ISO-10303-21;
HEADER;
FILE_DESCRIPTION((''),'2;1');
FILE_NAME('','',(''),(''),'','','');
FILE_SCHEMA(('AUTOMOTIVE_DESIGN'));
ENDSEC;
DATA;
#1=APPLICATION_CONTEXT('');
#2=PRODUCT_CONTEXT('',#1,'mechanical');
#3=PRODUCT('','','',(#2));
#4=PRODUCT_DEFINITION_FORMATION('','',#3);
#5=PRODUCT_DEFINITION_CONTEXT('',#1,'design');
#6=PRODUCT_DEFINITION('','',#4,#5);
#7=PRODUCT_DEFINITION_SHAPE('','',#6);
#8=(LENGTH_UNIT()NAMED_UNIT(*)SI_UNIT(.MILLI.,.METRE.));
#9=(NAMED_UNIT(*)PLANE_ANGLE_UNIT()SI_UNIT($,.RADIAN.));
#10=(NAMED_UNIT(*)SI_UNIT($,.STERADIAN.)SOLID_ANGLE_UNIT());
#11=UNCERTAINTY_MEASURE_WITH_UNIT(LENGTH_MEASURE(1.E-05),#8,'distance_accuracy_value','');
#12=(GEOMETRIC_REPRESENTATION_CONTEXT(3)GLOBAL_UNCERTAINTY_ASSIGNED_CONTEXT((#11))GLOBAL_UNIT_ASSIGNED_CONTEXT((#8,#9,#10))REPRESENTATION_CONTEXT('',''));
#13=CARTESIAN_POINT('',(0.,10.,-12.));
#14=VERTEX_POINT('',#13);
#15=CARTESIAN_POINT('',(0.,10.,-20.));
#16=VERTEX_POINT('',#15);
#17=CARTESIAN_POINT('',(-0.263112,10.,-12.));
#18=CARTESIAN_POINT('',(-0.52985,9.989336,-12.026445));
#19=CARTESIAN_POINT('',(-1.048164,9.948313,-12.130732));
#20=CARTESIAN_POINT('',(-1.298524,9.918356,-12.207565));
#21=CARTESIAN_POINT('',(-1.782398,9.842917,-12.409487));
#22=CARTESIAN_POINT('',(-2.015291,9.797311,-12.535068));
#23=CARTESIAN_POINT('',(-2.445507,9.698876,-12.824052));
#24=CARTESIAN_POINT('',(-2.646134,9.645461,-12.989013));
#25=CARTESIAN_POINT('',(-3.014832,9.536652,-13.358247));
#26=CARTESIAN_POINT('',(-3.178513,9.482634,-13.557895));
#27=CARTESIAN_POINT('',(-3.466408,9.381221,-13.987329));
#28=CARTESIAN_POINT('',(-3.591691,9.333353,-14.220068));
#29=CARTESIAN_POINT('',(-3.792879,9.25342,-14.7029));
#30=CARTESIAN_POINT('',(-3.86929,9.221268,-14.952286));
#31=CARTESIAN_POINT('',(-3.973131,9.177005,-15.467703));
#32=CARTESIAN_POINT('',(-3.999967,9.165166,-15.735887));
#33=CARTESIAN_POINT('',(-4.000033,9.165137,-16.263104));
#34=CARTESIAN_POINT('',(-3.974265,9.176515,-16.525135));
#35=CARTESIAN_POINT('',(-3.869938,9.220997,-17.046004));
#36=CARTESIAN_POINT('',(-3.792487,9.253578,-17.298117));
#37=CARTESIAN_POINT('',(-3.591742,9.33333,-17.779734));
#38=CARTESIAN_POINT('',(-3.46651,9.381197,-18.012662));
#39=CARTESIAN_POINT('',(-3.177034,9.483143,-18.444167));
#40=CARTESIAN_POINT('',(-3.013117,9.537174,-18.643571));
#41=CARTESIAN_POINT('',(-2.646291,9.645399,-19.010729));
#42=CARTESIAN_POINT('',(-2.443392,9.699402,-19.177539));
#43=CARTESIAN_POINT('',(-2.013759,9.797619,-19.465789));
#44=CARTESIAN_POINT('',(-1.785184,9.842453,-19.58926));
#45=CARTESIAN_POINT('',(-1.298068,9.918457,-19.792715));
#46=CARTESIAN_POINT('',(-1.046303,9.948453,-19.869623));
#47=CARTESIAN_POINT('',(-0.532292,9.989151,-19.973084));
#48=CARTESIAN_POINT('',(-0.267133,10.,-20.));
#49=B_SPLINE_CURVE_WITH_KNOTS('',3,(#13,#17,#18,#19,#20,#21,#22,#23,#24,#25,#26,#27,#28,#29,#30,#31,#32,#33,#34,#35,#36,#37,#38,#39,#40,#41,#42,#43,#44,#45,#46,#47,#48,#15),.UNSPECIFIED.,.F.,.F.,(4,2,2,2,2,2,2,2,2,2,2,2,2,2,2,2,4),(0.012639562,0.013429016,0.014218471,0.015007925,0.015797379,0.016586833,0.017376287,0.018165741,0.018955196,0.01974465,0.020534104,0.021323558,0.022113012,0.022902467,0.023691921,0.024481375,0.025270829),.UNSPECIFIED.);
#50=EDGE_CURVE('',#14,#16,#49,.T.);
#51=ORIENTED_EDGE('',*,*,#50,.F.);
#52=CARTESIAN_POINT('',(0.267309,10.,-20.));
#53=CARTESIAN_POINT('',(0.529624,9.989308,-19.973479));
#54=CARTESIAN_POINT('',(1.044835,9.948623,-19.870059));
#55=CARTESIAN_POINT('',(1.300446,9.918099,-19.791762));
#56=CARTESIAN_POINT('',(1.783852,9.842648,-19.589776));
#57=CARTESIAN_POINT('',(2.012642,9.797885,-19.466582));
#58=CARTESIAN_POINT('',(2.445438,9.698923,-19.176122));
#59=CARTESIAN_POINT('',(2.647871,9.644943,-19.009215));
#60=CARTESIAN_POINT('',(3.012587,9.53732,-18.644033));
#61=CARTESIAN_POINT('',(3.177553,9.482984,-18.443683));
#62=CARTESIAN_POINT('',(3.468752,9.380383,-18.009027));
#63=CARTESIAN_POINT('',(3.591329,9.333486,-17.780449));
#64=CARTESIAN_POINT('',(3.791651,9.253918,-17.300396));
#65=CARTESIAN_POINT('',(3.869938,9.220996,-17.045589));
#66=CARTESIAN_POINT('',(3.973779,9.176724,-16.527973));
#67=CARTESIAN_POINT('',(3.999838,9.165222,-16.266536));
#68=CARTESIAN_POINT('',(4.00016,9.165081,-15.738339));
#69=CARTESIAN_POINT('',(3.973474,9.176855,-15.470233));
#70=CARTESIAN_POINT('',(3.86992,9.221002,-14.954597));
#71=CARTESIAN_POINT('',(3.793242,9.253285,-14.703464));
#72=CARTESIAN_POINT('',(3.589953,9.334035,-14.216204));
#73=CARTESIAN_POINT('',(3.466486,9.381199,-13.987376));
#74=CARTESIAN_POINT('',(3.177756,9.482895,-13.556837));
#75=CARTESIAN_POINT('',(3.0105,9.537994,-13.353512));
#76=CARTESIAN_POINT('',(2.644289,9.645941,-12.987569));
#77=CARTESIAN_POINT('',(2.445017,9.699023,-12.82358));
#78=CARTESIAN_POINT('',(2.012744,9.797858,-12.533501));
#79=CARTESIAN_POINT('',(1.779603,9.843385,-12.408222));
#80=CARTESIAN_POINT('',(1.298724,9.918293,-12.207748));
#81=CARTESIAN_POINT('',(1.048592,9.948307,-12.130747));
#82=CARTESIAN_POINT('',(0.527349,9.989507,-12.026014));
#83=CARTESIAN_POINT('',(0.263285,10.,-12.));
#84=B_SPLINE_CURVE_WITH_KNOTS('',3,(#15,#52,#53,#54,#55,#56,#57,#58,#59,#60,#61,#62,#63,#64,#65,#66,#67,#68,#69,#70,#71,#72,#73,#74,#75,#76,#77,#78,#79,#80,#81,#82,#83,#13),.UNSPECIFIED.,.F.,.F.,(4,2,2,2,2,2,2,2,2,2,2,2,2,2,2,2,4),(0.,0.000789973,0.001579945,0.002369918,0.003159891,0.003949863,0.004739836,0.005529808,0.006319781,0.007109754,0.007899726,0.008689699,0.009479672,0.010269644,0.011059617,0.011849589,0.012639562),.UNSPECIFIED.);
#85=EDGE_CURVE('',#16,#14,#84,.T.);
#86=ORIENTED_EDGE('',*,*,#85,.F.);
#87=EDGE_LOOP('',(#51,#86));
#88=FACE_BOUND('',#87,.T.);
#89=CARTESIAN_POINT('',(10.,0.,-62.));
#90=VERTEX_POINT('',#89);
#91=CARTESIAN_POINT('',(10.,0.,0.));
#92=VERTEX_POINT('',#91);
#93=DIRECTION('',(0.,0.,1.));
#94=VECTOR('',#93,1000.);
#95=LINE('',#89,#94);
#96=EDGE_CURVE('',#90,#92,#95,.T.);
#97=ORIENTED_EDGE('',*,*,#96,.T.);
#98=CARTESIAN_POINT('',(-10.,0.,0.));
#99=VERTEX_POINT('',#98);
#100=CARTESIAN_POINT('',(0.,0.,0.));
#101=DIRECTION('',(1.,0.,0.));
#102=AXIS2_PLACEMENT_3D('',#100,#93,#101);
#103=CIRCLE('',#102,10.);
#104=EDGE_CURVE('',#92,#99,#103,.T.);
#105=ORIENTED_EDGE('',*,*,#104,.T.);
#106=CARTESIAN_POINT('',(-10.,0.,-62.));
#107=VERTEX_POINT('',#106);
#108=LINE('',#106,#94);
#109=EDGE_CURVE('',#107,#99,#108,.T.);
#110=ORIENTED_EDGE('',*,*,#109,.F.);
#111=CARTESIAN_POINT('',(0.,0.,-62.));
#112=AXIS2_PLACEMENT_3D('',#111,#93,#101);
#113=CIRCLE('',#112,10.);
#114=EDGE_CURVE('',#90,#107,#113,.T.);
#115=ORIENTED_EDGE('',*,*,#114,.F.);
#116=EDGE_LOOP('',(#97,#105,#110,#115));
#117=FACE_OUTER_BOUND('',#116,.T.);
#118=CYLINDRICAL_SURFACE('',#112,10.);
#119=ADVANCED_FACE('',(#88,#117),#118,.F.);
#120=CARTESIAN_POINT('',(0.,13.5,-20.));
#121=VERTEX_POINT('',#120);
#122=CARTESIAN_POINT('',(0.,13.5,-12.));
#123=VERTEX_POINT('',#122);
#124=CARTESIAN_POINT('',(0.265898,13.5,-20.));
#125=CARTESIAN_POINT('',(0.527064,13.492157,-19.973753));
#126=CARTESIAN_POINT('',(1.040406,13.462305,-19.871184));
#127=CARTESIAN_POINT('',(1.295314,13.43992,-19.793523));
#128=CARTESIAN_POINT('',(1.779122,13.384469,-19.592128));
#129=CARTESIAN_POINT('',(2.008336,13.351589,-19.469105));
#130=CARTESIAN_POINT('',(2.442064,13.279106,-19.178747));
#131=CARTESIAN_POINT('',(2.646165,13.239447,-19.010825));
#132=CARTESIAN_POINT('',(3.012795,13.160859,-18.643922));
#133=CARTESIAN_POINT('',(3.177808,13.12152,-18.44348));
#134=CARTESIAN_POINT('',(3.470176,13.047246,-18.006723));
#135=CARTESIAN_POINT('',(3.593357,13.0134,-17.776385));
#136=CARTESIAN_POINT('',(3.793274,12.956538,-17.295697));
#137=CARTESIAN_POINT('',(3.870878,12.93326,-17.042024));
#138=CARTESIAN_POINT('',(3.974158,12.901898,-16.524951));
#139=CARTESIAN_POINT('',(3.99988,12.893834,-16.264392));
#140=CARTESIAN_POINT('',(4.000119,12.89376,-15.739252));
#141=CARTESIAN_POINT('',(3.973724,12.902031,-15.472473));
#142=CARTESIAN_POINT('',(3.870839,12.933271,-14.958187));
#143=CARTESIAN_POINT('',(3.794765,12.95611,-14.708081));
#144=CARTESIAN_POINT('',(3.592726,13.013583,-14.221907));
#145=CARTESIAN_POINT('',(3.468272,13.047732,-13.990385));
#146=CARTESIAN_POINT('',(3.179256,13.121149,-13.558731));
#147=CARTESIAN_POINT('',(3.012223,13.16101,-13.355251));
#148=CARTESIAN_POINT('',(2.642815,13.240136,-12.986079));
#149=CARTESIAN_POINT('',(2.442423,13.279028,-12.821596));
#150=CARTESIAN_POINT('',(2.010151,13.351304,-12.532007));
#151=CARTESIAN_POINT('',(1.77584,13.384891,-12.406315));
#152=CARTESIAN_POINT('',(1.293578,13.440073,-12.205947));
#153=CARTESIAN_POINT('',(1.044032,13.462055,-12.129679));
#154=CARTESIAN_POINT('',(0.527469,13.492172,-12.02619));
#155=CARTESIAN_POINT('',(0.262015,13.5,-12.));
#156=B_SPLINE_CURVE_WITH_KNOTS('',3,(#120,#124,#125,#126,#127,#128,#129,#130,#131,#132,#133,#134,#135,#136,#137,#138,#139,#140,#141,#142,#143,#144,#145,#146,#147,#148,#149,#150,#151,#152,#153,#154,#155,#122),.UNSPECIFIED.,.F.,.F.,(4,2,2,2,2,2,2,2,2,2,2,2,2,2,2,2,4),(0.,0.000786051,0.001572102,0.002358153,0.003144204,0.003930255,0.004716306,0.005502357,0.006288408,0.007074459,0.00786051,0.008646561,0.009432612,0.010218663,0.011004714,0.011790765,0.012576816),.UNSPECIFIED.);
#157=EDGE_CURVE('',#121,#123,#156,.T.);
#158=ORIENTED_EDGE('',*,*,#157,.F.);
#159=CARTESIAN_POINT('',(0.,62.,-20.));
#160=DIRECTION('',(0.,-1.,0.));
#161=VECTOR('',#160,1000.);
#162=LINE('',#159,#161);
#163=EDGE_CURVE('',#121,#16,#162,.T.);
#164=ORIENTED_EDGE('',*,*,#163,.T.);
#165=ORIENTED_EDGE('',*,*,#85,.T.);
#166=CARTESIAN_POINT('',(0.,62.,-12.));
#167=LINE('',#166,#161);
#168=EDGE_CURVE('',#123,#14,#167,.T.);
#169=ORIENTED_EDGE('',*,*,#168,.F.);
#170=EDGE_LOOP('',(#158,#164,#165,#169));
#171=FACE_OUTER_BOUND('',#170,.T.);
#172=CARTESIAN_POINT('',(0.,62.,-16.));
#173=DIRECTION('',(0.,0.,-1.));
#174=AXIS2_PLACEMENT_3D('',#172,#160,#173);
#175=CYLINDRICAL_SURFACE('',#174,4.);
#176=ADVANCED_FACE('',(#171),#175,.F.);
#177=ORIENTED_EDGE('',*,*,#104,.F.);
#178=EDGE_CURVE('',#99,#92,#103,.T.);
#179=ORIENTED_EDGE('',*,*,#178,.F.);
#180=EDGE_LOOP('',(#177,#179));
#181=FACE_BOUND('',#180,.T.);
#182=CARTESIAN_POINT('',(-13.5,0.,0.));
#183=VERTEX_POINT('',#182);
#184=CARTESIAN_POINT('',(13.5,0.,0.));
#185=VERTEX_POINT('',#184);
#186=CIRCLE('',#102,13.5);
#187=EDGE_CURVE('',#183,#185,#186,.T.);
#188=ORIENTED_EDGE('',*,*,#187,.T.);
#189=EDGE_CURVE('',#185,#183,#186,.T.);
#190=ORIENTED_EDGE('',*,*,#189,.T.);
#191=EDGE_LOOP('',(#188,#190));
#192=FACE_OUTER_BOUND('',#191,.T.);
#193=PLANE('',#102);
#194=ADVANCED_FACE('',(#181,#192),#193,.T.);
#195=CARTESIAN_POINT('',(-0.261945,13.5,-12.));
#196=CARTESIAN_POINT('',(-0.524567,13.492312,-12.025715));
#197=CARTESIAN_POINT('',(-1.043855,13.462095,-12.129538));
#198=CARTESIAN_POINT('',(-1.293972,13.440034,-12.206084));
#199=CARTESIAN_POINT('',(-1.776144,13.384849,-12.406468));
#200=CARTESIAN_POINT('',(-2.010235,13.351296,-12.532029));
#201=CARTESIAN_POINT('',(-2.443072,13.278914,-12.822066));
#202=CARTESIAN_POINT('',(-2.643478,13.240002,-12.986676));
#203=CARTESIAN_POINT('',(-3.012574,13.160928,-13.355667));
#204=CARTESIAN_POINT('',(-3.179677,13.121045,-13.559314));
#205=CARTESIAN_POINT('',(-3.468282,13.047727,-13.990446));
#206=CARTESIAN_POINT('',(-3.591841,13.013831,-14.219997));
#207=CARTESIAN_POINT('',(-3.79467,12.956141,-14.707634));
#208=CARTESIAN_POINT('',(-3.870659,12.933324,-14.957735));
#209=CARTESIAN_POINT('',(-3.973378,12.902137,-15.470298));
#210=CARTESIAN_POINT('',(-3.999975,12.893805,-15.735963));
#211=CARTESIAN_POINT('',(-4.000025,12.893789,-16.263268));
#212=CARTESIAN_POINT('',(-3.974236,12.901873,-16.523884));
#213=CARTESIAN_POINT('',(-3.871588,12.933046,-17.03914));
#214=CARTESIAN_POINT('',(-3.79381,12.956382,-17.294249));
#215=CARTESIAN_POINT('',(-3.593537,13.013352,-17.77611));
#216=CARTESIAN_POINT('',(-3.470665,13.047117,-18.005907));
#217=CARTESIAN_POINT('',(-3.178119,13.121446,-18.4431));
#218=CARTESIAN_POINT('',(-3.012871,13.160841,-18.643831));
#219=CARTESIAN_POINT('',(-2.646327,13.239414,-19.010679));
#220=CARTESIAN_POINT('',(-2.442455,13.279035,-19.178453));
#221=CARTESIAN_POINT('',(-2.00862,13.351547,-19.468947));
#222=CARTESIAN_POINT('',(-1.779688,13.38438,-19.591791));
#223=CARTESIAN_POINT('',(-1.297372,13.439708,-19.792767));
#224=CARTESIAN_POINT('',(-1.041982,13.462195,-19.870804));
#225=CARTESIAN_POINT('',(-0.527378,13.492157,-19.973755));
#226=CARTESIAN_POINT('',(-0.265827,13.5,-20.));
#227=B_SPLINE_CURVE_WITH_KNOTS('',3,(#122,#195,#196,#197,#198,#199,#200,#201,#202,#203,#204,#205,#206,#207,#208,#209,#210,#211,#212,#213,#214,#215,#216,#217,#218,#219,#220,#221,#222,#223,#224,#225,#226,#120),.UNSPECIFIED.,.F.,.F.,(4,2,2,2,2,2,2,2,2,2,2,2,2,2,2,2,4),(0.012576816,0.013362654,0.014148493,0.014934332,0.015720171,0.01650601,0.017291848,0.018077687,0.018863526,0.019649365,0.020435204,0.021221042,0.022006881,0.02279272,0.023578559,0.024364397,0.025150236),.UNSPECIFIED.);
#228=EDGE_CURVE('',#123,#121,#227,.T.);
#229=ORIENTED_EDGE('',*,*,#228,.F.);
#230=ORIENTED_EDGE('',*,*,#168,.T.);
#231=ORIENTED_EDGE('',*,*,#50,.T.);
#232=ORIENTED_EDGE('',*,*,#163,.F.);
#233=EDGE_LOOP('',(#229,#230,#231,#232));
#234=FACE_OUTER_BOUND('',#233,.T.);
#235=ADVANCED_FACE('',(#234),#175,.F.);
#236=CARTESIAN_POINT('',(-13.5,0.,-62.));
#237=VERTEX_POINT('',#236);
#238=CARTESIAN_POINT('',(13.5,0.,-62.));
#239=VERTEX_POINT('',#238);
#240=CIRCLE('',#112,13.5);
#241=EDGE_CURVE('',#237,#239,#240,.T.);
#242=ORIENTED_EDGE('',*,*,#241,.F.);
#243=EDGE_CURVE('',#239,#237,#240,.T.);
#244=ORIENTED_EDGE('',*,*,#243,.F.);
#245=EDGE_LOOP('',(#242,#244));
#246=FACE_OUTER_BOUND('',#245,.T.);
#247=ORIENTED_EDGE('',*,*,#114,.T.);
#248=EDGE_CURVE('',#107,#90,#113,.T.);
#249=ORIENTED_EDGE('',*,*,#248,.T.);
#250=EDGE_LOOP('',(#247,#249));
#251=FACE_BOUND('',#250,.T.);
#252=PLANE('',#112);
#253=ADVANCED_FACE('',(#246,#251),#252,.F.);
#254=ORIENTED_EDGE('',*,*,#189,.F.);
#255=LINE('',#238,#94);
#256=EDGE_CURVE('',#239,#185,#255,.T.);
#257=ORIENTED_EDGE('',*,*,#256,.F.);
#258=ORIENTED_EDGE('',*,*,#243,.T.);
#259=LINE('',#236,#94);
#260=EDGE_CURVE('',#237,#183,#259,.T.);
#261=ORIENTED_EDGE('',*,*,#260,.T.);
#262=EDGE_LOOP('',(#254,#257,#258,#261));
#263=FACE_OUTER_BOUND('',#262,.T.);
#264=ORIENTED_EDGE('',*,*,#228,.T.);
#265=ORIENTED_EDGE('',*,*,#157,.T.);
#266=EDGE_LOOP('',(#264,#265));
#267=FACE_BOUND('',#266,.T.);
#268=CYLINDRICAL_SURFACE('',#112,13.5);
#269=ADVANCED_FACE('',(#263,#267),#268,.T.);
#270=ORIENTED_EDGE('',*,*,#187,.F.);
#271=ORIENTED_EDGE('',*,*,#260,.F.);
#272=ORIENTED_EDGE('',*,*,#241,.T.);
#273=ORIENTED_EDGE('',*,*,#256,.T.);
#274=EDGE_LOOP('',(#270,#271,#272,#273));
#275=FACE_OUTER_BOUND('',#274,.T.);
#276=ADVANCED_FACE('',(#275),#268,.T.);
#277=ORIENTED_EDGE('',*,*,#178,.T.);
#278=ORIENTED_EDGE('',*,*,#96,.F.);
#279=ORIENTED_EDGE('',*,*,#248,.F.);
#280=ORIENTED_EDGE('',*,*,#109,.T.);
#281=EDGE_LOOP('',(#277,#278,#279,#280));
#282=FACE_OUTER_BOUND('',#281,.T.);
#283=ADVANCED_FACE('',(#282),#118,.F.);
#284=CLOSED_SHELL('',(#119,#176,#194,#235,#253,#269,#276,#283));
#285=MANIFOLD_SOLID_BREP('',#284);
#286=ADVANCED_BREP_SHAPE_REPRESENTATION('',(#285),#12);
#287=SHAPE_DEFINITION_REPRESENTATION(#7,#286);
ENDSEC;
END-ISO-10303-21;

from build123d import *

# Parameters (mm, degrees)
SKETCH1_R           = 13.5
SKETCH1_R_2         = 10
BOSS_EXTRUDE1_DEPTH = 62
SKETCH2_R           = 4
CUT_EXTRUDE1_DEPTH  = 62


with BuildPart() as part:
    # Sketch1 → Boss-Extrude1 (new body)
    with BuildSketch(Plane.XY):
        Circle(SKETCH1_R)
        Circle(SKETCH1_R_2, mode=Mode.SUBTRACT)
    extrude(amount=-BOSS_EXTRUDE1_DEPTH)

    # Sketch2 → Cut-Extrude1 (cut)
    with BuildSketch(Plane(origin=(0, 0, 0), x_dir=(1, 0, 0), z_dir=(0, 1, 0))):
        with Locations(Location((0, 16, 0), (0, 0, 90))):
            Circle(SKETCH2_R)
    extrude(amount=CUT_EXTRUDE1_DEPTH, mode=Mode.SUBTRACT)


solid = part.part
